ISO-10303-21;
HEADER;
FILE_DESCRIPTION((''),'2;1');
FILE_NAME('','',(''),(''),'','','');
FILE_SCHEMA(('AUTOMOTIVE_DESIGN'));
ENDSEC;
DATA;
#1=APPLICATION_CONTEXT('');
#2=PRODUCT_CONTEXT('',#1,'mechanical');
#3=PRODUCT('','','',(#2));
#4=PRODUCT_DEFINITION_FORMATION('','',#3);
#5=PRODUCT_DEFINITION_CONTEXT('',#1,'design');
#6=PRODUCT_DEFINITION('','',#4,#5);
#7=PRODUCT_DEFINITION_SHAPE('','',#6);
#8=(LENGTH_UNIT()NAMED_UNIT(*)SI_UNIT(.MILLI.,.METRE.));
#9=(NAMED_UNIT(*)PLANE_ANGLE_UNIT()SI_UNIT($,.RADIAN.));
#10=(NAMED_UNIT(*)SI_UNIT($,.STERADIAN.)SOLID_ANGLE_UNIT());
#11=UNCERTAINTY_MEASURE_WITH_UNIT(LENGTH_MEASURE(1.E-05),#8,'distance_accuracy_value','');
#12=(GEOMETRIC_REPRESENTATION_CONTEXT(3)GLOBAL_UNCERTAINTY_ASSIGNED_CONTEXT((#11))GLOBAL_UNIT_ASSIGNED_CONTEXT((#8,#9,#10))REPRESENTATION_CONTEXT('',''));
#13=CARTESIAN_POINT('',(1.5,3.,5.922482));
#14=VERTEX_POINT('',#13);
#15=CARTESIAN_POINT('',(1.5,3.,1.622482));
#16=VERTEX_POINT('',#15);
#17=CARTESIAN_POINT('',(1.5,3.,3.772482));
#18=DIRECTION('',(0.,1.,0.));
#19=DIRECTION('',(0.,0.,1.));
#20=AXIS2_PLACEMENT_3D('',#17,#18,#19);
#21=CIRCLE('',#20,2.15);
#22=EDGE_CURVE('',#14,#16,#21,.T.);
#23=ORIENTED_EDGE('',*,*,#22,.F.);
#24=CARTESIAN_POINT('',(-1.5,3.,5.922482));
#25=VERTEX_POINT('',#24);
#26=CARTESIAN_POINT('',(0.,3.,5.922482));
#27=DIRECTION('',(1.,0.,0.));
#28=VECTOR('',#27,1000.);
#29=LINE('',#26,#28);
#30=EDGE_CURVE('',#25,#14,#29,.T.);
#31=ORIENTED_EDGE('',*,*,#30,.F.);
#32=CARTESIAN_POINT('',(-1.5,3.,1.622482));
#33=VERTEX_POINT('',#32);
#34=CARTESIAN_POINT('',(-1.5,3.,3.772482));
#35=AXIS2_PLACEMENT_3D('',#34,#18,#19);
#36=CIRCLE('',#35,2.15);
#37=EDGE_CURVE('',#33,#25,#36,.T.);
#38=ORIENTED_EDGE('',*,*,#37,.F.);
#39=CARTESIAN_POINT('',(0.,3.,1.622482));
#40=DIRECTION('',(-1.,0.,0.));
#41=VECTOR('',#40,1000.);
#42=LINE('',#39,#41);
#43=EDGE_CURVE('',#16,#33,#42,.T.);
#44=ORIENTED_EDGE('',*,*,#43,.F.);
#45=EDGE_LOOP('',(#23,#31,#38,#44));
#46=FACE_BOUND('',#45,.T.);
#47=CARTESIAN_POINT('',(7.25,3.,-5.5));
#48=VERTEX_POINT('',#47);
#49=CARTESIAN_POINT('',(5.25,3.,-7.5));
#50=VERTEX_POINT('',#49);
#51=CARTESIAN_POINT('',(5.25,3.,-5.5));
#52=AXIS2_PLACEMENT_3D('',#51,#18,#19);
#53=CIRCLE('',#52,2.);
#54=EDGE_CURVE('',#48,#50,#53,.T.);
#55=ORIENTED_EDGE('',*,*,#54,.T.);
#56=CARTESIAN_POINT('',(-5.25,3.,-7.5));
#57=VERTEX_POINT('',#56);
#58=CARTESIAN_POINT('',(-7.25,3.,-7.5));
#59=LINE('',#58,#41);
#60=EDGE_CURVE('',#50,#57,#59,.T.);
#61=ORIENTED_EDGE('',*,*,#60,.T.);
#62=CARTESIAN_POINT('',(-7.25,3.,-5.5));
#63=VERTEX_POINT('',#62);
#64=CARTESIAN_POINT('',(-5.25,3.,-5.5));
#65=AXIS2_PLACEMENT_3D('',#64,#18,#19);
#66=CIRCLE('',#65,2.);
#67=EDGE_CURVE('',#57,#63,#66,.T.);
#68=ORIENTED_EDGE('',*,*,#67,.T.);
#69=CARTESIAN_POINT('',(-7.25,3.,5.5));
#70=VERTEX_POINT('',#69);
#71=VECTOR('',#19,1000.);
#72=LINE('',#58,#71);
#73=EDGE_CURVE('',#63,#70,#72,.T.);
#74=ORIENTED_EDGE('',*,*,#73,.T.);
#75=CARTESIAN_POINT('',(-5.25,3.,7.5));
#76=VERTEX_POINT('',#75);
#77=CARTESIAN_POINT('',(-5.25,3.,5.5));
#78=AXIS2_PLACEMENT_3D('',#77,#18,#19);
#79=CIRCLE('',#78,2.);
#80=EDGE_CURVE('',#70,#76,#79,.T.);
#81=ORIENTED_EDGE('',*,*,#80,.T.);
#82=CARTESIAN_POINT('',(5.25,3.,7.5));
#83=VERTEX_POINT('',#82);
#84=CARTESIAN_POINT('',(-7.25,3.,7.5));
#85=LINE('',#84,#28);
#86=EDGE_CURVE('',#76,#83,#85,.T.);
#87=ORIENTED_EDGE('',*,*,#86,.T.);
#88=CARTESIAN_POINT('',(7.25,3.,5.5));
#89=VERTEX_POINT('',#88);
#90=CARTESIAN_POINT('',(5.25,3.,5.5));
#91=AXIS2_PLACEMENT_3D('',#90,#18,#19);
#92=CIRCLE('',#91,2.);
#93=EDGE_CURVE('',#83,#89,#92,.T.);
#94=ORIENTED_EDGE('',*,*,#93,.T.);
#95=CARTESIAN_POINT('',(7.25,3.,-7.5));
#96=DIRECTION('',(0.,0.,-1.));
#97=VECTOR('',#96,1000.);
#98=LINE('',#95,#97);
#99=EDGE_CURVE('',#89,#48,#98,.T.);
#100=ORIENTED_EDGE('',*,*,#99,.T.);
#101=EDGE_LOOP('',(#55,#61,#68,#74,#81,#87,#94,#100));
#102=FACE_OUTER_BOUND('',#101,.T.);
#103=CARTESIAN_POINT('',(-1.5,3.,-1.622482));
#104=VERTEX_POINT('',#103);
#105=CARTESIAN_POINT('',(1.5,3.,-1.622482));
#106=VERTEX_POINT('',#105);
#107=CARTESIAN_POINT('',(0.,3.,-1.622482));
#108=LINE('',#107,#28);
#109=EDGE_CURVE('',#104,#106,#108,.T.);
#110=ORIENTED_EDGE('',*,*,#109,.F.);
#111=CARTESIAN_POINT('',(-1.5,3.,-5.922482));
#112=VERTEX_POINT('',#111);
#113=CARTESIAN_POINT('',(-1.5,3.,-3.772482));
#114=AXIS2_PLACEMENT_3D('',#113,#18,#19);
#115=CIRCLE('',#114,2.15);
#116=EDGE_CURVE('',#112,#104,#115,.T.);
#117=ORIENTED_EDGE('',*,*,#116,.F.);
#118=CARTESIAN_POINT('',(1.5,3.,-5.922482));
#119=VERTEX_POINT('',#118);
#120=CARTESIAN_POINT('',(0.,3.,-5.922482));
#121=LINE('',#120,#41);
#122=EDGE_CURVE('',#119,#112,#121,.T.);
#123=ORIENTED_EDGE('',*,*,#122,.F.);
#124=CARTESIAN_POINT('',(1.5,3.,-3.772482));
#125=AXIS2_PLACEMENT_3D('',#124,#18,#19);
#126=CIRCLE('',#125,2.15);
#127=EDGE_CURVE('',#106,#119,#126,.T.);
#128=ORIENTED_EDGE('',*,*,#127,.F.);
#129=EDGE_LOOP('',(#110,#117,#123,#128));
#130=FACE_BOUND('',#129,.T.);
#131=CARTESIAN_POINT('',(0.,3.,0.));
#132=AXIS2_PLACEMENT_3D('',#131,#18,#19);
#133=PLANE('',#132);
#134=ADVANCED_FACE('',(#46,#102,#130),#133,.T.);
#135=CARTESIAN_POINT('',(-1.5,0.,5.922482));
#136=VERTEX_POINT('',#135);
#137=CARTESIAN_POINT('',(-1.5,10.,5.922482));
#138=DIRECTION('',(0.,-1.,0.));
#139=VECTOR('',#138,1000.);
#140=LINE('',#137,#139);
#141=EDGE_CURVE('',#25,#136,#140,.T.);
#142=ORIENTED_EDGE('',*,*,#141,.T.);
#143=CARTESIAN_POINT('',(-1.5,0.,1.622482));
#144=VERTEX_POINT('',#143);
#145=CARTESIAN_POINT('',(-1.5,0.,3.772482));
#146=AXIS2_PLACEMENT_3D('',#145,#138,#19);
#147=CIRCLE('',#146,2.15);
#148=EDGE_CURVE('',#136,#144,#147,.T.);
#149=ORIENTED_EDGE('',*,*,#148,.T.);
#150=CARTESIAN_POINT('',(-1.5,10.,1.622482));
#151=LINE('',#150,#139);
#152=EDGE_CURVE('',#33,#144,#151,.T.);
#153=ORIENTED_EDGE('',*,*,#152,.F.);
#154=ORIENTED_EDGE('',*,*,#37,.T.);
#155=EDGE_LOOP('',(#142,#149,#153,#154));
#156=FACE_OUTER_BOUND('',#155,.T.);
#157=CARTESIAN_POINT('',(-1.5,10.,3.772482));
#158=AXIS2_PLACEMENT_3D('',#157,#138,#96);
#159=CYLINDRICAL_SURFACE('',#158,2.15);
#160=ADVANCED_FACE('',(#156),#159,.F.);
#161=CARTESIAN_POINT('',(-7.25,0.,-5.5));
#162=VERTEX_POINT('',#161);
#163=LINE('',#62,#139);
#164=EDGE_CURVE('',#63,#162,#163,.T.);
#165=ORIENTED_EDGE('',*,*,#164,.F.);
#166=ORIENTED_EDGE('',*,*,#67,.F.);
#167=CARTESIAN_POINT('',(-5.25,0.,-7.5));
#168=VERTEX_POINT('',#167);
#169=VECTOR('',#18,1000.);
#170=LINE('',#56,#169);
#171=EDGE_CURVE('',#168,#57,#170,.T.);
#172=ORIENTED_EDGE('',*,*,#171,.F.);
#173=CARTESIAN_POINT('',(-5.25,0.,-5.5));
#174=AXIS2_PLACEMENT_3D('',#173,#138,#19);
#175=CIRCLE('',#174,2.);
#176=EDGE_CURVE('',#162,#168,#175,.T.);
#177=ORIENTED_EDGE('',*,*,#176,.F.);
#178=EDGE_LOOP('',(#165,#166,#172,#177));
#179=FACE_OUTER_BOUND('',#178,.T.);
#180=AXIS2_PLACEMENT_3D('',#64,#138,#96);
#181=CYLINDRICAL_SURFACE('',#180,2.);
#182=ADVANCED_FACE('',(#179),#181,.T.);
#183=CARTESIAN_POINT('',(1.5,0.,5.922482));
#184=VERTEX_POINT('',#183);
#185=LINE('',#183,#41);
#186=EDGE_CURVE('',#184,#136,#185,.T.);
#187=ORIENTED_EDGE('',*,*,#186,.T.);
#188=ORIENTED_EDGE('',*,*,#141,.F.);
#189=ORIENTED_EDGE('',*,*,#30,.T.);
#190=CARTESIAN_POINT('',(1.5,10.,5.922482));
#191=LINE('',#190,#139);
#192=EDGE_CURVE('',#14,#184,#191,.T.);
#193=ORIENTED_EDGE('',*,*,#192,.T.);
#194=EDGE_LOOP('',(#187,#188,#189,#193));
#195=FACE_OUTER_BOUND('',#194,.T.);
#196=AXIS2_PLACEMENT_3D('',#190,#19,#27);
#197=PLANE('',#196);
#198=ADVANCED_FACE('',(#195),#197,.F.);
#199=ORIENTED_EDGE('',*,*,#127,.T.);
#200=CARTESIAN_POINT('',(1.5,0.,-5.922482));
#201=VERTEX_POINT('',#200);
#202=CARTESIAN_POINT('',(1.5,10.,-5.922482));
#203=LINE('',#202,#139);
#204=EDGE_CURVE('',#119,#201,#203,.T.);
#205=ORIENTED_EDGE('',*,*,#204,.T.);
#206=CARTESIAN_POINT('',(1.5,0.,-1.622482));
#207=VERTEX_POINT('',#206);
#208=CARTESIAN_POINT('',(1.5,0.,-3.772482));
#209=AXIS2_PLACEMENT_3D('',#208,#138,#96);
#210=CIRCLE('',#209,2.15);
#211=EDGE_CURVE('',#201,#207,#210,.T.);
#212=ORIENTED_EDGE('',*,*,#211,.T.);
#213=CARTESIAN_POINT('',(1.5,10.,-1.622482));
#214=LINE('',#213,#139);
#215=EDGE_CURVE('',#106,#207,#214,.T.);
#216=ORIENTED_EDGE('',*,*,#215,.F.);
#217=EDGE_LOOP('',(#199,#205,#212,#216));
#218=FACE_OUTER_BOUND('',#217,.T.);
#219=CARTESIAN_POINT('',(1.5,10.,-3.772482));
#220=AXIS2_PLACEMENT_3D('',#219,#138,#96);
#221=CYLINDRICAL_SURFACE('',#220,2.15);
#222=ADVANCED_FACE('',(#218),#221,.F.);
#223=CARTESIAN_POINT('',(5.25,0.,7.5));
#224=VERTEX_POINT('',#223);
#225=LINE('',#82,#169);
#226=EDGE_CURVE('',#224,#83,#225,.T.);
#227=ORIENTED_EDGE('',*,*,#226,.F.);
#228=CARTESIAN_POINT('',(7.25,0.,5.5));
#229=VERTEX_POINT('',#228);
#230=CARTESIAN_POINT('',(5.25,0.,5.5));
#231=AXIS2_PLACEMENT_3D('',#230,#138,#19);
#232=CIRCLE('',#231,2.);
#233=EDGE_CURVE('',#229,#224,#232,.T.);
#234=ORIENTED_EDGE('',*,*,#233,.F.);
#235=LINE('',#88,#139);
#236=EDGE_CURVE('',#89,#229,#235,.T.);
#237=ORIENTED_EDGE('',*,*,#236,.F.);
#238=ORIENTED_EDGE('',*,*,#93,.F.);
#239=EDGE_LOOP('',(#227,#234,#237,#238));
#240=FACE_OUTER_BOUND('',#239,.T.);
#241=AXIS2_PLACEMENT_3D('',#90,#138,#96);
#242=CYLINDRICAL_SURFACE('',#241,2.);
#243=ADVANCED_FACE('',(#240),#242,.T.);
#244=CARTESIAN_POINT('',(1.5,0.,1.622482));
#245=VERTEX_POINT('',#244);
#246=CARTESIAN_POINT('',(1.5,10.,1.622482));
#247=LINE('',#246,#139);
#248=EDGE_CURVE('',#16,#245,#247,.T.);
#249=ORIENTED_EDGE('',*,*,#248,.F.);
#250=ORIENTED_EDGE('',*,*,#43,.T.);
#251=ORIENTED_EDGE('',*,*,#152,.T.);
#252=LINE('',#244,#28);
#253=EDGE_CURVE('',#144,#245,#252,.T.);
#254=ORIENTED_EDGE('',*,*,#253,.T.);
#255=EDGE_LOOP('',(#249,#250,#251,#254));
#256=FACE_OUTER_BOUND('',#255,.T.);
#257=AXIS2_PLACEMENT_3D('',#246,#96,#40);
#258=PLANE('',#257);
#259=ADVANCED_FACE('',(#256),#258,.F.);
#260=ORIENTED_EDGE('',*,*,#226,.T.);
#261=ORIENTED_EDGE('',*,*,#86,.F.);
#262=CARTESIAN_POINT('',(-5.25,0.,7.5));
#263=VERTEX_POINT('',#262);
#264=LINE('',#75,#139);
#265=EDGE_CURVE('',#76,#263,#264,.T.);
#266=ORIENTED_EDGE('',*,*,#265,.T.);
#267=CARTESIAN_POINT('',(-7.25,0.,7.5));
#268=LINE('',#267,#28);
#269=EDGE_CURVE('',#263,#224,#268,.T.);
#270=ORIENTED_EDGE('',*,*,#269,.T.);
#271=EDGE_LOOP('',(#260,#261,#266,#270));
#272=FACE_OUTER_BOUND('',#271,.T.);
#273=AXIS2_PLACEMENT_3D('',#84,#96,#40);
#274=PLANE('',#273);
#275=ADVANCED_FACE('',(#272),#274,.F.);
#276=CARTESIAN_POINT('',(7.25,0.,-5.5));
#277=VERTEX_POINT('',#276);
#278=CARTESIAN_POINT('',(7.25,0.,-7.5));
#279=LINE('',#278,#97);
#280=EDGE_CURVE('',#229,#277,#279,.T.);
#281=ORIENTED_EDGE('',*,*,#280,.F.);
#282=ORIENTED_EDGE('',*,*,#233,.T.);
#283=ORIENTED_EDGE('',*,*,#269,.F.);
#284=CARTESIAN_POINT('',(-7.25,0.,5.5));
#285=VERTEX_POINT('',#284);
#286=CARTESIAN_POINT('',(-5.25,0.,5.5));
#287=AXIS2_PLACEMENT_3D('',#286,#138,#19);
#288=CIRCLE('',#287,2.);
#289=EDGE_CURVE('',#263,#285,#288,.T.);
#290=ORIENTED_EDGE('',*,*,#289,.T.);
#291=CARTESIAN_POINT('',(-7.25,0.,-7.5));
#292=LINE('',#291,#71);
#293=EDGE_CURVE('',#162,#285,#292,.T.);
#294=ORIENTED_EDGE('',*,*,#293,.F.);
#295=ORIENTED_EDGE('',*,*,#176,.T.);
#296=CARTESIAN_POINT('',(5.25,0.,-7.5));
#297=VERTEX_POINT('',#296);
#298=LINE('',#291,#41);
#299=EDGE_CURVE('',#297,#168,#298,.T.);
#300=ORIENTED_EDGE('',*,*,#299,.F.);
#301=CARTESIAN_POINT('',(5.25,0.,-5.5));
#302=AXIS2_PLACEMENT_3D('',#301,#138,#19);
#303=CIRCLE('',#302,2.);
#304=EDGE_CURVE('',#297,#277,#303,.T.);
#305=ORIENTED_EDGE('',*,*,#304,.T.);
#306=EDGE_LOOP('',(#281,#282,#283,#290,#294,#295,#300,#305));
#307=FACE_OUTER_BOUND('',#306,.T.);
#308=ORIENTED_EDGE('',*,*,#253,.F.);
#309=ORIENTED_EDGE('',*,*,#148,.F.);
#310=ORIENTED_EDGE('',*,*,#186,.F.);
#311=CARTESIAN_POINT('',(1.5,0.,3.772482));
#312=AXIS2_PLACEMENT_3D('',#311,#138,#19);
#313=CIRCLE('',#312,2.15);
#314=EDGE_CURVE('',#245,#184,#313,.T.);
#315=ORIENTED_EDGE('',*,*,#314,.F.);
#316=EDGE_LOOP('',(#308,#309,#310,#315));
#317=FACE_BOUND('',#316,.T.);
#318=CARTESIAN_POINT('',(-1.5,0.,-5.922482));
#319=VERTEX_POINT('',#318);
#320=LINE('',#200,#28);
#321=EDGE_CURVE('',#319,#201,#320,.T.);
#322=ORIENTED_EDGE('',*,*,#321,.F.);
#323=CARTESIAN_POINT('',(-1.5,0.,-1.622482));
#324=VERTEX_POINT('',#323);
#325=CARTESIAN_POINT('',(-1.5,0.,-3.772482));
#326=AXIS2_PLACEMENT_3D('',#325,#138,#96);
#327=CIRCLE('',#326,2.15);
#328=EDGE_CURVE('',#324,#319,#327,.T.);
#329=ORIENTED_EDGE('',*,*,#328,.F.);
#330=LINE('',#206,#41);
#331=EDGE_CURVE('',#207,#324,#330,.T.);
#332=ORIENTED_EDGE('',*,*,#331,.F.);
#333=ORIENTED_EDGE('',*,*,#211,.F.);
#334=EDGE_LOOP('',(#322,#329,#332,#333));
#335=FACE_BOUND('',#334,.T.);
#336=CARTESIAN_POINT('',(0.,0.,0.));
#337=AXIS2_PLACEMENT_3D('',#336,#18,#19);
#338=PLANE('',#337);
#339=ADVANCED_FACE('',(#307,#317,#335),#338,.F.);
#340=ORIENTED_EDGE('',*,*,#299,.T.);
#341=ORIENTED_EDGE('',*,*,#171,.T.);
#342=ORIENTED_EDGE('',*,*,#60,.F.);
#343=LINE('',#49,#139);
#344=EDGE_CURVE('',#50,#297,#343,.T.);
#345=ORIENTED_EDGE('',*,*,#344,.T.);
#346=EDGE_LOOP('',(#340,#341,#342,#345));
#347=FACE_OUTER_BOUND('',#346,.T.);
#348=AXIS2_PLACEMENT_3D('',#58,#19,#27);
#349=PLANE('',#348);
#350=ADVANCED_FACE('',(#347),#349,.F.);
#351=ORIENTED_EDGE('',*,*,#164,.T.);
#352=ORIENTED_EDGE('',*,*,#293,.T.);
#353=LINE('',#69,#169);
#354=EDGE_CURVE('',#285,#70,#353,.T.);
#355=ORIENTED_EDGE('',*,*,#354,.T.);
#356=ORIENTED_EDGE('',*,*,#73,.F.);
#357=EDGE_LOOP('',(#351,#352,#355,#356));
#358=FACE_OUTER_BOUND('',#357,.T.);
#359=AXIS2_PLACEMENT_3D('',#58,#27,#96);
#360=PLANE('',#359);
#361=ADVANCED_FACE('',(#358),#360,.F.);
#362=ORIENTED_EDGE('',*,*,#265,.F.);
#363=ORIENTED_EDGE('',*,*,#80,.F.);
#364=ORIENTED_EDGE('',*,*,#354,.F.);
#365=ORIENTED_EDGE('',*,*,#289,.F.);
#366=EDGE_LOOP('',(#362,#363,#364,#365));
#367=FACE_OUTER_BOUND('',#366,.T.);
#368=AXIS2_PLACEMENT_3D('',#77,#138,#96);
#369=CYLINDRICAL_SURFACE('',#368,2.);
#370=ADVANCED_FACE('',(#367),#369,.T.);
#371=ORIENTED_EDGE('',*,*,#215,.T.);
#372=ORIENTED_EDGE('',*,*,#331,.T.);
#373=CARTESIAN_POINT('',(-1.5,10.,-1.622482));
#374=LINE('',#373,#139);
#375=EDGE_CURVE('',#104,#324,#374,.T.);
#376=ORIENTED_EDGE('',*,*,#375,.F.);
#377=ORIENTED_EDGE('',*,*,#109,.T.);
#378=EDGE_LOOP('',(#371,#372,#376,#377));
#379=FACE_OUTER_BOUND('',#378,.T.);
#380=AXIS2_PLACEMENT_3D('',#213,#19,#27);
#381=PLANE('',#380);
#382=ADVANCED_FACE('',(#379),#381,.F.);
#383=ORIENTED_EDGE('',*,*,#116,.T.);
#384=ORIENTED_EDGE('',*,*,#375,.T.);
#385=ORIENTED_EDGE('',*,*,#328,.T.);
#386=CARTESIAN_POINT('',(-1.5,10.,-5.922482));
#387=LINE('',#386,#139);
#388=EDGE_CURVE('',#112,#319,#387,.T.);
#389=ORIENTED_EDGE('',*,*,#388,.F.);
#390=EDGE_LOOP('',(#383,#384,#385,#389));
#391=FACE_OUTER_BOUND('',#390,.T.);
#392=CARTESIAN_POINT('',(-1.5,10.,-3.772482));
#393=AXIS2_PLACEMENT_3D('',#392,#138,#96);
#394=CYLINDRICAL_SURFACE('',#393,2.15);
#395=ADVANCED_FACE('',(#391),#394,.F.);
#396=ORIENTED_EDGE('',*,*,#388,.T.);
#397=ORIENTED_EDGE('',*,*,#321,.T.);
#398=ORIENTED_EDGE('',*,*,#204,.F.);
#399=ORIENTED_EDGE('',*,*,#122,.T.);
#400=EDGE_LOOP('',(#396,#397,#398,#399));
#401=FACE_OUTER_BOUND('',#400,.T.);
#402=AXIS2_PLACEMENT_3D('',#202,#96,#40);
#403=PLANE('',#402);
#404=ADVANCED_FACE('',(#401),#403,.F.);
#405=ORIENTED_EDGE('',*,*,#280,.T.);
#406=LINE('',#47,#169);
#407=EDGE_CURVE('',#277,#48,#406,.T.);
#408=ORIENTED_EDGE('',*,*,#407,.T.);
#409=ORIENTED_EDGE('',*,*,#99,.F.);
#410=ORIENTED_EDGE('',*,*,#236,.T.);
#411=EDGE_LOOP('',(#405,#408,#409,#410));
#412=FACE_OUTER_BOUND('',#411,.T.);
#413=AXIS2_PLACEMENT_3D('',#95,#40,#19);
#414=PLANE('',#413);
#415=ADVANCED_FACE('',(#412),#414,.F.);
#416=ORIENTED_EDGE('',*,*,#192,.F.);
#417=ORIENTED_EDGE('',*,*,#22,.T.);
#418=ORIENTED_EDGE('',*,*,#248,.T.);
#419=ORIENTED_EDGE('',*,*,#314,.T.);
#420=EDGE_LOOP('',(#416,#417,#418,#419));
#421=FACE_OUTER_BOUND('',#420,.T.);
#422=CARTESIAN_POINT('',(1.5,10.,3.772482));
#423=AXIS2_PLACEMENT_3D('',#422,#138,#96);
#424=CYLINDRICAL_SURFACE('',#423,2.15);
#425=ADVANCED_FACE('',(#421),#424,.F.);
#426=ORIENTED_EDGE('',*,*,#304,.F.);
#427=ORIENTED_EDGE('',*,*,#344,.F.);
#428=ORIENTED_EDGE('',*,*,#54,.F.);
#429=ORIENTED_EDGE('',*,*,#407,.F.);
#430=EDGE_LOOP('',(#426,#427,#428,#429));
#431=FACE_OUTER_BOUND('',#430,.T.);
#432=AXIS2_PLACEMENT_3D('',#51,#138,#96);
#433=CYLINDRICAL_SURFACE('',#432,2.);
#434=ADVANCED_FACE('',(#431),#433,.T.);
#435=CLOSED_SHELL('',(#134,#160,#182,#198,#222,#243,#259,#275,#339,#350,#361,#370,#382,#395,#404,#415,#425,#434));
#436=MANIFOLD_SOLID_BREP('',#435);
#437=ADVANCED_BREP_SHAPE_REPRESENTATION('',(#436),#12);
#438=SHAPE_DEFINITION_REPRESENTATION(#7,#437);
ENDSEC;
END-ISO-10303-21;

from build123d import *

# Parameters (mm, degrees)
SKETCH_1_W          = 14.5
SKETCH_1_H          = 15
EXTRUDE_1_DEPTH     = 3
CUT_EXTRUDE_1_DEPTH = 10
FILLET_1_R          = 2


with BuildPart() as part:
    # 草图1 → 凸台-拉伸1 (new body)
    with BuildSketch(Plane(origin=(0, 0, 0), x_dir=(1, 0, 0), z_dir=(0, 1, 0))):
        Rectangle(SKETCH_1_W, SKETCH_1_H)
    extrude(amount=EXTRUDE_1_DEPTH)

    # 草图4 → 切除-拉伸1 (cut)
    with BuildSketch(Plane.XZ):
        with BuildLine():
            Line((1.5, -5.922481842), (-1.5, -5.922481842))
            ThreePointArc((-1.5, -5.922481842), (-3.65, -3.772481842), (-1.5, -1.622481842))
            Line((-1.5, -1.622481842), (1.5, -1.622481842))
            ThreePointArc((1.5, -1.622481842), (3.65, -3.772481842), (1.5, -5.922481842))
        make_face()
        with BuildLine():
            Line((1.5, 5.922481842), (-1.5, 5.922481842))
            ThreePointArc((-1.5, 5.922481842), (-3.65, 3.772481842), (-1.5, 1.622481842))
            Line((-1.5, 1.622481842), (1.5, 1.622481842))
            ThreePointArc((1.5, 1.622481842), (3.65, 3.772481842), (1.5, 5.922481842))
        make_face()
    extrude(amount=-CUT_EXTRUDE_1_DEPTH, mode=Mode.SUBTRACT)

    # 圆角1
    fillet_1_edges = [part.edges().sort_by_distance(p)[0] for p in [
        (7.25, 1.5, 7.5),
        (-7.25, 1.5, 7.5),
        (-7.25, 1.5, -7.5),
        (7.25, 1.5, -7.5),
    ]]
    fillet(fillet_1_edges, radius=FILLET_1_R)


solid = part.part
